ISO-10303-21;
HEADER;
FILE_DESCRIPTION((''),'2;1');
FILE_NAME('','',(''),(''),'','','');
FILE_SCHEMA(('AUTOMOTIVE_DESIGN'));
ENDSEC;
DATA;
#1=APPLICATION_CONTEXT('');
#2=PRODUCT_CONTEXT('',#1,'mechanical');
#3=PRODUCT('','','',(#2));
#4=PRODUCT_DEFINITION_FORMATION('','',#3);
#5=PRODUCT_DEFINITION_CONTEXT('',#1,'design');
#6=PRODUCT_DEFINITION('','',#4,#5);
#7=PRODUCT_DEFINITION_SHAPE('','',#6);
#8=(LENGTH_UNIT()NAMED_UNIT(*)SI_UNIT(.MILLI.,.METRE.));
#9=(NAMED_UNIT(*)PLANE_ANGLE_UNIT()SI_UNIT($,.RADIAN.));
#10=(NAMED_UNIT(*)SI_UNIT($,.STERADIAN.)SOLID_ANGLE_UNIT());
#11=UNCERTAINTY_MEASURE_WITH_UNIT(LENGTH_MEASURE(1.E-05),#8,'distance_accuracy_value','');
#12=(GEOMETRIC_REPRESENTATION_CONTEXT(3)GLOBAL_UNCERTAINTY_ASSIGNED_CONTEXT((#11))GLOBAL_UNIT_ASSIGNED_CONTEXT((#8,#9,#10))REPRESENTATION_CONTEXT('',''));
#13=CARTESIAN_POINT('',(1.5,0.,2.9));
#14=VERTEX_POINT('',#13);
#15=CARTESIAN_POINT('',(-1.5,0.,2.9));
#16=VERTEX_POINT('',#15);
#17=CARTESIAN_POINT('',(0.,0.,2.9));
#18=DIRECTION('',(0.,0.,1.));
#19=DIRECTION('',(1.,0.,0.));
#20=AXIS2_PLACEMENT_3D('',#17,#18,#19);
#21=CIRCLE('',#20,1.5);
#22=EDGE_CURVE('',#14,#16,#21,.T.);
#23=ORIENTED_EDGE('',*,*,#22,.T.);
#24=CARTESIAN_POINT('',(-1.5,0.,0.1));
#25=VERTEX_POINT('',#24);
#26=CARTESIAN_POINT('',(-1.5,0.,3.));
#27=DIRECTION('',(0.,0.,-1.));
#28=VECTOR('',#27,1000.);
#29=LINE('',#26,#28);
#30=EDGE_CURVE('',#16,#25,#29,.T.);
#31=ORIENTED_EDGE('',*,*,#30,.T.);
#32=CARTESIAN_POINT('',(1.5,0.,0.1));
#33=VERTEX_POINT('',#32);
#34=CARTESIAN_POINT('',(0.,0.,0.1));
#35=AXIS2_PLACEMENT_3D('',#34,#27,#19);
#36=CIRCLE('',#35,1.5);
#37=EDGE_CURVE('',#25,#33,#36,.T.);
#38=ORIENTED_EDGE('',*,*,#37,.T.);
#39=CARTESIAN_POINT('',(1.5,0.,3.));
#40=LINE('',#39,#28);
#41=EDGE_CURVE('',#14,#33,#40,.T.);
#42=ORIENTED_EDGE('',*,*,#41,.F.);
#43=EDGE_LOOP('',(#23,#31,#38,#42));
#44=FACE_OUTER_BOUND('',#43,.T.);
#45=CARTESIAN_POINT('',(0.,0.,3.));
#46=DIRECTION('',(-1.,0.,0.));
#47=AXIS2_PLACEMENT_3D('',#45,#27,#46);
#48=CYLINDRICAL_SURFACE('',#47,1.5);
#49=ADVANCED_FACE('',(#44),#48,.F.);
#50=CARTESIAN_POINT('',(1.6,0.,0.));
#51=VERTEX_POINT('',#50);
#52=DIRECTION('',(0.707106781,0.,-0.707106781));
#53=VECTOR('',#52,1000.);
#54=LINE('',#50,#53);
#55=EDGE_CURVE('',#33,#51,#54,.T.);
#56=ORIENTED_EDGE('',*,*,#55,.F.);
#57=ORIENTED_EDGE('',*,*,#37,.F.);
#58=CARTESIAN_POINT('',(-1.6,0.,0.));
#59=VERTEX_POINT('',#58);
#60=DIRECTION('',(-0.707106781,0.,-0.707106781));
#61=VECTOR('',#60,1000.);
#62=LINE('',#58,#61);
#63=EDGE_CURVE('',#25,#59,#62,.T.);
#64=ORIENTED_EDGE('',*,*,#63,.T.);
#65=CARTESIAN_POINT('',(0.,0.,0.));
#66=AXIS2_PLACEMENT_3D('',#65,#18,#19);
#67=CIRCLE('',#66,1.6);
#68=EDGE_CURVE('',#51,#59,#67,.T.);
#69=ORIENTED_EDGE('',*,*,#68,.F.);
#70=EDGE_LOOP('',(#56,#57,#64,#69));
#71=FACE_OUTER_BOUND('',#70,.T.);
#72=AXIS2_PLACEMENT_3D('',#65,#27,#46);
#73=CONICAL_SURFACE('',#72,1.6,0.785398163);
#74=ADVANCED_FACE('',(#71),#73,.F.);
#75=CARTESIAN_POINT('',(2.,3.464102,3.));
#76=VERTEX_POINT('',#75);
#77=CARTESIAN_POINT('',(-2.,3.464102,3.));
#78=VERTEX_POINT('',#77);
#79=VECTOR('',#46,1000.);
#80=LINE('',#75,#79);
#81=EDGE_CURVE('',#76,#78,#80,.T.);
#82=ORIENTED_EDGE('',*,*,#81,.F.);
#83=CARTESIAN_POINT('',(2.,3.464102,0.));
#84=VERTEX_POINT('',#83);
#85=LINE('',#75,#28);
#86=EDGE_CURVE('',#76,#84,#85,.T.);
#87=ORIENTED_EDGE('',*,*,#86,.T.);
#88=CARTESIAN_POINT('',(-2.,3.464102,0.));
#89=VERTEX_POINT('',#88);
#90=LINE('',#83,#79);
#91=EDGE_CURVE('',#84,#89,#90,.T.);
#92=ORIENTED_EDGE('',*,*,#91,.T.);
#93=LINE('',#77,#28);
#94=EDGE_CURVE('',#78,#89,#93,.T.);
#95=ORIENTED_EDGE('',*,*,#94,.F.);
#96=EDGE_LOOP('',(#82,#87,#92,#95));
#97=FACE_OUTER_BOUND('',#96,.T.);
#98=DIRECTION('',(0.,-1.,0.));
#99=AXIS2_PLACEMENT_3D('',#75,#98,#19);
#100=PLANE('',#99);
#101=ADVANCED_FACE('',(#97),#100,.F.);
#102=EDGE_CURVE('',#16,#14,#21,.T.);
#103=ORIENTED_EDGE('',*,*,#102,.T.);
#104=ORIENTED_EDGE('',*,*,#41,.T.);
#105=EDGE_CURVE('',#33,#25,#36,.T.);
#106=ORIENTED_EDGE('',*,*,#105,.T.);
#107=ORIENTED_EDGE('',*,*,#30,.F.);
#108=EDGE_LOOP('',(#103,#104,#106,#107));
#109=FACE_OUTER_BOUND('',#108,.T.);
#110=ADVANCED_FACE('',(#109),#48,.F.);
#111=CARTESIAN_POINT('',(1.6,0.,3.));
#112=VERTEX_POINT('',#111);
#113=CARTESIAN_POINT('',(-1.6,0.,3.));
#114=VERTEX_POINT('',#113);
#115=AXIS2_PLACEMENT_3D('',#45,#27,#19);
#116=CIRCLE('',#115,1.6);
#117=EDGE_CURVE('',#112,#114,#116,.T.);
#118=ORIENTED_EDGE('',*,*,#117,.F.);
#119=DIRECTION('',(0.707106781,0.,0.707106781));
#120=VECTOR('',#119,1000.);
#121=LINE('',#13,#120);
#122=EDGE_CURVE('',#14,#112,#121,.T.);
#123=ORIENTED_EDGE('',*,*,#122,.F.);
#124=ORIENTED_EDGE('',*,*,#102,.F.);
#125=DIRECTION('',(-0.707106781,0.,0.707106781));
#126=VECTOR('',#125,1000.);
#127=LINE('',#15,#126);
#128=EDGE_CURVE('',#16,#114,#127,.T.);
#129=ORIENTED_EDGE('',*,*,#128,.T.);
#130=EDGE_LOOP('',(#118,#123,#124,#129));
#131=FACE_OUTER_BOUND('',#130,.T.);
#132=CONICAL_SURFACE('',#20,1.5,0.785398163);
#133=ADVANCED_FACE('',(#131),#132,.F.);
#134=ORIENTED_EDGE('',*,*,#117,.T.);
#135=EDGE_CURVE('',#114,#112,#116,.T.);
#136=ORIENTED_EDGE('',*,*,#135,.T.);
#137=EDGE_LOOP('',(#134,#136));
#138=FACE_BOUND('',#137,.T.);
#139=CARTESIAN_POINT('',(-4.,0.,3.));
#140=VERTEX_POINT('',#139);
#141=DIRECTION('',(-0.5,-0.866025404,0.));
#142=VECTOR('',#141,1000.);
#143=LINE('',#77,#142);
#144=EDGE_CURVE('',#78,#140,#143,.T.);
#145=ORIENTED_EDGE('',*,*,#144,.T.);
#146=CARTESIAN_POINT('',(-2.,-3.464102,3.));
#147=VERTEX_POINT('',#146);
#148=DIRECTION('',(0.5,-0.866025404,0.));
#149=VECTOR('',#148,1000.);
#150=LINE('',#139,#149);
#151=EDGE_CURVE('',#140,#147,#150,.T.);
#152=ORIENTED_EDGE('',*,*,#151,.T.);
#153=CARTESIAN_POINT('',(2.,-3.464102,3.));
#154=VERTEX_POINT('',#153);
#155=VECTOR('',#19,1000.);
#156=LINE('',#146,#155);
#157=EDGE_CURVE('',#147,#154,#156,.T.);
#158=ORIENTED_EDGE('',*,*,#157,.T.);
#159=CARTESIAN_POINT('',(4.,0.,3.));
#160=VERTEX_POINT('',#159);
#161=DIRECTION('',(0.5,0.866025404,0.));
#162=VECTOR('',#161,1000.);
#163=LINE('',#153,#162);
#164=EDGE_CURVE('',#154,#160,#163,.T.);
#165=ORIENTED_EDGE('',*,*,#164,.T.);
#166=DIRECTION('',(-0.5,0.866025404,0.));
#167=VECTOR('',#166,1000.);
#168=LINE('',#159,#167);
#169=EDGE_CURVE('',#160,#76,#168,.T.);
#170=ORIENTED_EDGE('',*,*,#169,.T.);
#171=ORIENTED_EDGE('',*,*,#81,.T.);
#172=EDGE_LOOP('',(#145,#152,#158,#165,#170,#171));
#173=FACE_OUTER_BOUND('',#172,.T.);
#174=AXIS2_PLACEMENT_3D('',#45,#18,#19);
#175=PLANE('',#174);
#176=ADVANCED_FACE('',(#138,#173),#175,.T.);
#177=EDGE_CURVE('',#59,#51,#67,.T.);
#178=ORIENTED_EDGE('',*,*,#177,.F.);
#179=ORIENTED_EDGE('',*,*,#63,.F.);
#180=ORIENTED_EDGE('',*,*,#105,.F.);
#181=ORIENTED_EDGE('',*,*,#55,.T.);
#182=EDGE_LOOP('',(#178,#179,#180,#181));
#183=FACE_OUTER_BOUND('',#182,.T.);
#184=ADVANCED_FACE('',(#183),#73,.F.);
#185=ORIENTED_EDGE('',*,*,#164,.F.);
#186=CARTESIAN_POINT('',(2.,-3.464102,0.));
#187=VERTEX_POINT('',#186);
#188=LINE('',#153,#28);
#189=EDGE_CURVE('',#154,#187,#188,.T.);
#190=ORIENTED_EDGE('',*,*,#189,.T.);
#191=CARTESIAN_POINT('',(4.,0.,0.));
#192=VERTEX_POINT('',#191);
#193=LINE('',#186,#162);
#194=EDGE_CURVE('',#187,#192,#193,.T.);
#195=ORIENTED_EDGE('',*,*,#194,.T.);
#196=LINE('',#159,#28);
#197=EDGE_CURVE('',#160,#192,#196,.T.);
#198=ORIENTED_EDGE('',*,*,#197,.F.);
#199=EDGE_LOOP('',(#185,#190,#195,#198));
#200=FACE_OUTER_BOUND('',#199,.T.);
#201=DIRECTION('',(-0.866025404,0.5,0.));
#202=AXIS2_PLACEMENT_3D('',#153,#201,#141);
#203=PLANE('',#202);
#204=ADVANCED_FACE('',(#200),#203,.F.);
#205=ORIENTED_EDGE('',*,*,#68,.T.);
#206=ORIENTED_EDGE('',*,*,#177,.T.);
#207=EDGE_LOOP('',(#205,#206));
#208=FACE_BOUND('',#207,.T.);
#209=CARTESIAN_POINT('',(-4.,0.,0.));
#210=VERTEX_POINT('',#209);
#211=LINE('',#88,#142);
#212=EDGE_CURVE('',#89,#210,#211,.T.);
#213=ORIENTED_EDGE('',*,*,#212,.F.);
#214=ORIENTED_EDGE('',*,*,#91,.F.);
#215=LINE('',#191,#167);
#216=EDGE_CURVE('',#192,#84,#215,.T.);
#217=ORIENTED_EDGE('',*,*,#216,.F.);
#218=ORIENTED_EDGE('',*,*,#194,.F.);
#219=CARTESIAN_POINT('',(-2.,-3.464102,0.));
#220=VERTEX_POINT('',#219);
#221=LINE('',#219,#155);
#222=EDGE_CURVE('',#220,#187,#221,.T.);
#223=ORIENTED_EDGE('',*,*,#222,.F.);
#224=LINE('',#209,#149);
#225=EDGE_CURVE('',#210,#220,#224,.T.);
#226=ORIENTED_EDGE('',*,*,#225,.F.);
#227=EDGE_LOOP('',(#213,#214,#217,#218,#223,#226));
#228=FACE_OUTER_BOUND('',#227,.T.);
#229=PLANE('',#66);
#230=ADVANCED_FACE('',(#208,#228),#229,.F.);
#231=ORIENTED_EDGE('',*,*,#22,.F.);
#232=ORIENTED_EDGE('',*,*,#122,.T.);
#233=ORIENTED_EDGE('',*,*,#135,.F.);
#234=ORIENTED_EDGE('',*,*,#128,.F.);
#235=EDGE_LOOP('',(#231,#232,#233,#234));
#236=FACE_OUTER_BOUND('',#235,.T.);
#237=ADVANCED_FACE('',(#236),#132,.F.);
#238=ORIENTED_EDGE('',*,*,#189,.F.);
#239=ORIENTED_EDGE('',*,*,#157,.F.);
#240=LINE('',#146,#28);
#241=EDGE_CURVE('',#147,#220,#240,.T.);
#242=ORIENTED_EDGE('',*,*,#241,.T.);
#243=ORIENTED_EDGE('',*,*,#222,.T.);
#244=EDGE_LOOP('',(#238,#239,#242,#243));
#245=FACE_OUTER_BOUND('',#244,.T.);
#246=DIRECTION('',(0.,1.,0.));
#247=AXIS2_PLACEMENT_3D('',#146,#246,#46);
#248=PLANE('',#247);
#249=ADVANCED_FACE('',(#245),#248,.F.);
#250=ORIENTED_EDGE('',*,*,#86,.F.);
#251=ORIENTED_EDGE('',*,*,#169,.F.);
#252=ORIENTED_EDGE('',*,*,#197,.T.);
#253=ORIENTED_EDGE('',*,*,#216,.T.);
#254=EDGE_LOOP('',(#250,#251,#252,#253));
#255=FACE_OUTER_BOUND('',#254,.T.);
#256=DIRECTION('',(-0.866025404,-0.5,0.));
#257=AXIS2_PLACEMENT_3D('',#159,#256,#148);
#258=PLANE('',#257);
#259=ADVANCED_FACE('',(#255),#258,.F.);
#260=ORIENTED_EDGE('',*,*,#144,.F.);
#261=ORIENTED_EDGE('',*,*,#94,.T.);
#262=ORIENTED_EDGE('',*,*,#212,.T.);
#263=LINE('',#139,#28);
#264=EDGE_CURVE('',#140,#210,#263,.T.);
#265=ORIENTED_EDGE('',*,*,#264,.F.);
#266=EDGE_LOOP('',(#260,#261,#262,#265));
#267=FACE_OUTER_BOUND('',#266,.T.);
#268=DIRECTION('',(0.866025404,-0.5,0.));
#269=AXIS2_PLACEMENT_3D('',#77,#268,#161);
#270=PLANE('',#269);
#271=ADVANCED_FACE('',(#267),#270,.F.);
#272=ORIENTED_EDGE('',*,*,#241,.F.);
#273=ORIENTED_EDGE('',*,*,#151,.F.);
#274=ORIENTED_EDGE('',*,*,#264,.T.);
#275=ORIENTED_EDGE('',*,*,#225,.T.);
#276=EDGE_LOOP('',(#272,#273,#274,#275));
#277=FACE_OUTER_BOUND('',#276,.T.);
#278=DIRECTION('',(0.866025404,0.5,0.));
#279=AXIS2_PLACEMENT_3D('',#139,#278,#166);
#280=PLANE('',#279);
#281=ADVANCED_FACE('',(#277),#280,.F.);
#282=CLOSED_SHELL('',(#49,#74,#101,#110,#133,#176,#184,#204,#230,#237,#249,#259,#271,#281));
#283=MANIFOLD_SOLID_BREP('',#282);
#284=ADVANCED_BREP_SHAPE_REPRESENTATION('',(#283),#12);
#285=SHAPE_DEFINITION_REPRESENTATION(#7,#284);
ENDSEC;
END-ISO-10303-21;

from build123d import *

# Parameters (mm, degrees)
SKETCH1_R           = 1.5
BOSS_EXTRUDE1_DEPTH = 3
CHAMFER1_SIZE       = 0.1


with BuildPart() as part:
    # Sketch1 → Boss-Extrude1 (new body)
    with BuildSketch(Plane.XY):
        Polygon((2, -3.464101615), (4, 0), (2, 3.464101615), (-2, 3.464101615), (-4, 0), (-2, -3.464101615), align=None)
        Circle(SKETCH1_R, mode=Mode.SUBTRACT)
    extrude(amount=BOSS_EXTRUDE1_DEPTH)

    # Chamfer1
    chamfer1_edges = [part.edges().sort_by_distance(p)[0] for p in [
        (-1.5, 0, 0),
        (-1.5, 0, 3),
    ]]
    chamfer(chamfer1_edges, length=CHAMFER1_SIZE)


solid = part.part
